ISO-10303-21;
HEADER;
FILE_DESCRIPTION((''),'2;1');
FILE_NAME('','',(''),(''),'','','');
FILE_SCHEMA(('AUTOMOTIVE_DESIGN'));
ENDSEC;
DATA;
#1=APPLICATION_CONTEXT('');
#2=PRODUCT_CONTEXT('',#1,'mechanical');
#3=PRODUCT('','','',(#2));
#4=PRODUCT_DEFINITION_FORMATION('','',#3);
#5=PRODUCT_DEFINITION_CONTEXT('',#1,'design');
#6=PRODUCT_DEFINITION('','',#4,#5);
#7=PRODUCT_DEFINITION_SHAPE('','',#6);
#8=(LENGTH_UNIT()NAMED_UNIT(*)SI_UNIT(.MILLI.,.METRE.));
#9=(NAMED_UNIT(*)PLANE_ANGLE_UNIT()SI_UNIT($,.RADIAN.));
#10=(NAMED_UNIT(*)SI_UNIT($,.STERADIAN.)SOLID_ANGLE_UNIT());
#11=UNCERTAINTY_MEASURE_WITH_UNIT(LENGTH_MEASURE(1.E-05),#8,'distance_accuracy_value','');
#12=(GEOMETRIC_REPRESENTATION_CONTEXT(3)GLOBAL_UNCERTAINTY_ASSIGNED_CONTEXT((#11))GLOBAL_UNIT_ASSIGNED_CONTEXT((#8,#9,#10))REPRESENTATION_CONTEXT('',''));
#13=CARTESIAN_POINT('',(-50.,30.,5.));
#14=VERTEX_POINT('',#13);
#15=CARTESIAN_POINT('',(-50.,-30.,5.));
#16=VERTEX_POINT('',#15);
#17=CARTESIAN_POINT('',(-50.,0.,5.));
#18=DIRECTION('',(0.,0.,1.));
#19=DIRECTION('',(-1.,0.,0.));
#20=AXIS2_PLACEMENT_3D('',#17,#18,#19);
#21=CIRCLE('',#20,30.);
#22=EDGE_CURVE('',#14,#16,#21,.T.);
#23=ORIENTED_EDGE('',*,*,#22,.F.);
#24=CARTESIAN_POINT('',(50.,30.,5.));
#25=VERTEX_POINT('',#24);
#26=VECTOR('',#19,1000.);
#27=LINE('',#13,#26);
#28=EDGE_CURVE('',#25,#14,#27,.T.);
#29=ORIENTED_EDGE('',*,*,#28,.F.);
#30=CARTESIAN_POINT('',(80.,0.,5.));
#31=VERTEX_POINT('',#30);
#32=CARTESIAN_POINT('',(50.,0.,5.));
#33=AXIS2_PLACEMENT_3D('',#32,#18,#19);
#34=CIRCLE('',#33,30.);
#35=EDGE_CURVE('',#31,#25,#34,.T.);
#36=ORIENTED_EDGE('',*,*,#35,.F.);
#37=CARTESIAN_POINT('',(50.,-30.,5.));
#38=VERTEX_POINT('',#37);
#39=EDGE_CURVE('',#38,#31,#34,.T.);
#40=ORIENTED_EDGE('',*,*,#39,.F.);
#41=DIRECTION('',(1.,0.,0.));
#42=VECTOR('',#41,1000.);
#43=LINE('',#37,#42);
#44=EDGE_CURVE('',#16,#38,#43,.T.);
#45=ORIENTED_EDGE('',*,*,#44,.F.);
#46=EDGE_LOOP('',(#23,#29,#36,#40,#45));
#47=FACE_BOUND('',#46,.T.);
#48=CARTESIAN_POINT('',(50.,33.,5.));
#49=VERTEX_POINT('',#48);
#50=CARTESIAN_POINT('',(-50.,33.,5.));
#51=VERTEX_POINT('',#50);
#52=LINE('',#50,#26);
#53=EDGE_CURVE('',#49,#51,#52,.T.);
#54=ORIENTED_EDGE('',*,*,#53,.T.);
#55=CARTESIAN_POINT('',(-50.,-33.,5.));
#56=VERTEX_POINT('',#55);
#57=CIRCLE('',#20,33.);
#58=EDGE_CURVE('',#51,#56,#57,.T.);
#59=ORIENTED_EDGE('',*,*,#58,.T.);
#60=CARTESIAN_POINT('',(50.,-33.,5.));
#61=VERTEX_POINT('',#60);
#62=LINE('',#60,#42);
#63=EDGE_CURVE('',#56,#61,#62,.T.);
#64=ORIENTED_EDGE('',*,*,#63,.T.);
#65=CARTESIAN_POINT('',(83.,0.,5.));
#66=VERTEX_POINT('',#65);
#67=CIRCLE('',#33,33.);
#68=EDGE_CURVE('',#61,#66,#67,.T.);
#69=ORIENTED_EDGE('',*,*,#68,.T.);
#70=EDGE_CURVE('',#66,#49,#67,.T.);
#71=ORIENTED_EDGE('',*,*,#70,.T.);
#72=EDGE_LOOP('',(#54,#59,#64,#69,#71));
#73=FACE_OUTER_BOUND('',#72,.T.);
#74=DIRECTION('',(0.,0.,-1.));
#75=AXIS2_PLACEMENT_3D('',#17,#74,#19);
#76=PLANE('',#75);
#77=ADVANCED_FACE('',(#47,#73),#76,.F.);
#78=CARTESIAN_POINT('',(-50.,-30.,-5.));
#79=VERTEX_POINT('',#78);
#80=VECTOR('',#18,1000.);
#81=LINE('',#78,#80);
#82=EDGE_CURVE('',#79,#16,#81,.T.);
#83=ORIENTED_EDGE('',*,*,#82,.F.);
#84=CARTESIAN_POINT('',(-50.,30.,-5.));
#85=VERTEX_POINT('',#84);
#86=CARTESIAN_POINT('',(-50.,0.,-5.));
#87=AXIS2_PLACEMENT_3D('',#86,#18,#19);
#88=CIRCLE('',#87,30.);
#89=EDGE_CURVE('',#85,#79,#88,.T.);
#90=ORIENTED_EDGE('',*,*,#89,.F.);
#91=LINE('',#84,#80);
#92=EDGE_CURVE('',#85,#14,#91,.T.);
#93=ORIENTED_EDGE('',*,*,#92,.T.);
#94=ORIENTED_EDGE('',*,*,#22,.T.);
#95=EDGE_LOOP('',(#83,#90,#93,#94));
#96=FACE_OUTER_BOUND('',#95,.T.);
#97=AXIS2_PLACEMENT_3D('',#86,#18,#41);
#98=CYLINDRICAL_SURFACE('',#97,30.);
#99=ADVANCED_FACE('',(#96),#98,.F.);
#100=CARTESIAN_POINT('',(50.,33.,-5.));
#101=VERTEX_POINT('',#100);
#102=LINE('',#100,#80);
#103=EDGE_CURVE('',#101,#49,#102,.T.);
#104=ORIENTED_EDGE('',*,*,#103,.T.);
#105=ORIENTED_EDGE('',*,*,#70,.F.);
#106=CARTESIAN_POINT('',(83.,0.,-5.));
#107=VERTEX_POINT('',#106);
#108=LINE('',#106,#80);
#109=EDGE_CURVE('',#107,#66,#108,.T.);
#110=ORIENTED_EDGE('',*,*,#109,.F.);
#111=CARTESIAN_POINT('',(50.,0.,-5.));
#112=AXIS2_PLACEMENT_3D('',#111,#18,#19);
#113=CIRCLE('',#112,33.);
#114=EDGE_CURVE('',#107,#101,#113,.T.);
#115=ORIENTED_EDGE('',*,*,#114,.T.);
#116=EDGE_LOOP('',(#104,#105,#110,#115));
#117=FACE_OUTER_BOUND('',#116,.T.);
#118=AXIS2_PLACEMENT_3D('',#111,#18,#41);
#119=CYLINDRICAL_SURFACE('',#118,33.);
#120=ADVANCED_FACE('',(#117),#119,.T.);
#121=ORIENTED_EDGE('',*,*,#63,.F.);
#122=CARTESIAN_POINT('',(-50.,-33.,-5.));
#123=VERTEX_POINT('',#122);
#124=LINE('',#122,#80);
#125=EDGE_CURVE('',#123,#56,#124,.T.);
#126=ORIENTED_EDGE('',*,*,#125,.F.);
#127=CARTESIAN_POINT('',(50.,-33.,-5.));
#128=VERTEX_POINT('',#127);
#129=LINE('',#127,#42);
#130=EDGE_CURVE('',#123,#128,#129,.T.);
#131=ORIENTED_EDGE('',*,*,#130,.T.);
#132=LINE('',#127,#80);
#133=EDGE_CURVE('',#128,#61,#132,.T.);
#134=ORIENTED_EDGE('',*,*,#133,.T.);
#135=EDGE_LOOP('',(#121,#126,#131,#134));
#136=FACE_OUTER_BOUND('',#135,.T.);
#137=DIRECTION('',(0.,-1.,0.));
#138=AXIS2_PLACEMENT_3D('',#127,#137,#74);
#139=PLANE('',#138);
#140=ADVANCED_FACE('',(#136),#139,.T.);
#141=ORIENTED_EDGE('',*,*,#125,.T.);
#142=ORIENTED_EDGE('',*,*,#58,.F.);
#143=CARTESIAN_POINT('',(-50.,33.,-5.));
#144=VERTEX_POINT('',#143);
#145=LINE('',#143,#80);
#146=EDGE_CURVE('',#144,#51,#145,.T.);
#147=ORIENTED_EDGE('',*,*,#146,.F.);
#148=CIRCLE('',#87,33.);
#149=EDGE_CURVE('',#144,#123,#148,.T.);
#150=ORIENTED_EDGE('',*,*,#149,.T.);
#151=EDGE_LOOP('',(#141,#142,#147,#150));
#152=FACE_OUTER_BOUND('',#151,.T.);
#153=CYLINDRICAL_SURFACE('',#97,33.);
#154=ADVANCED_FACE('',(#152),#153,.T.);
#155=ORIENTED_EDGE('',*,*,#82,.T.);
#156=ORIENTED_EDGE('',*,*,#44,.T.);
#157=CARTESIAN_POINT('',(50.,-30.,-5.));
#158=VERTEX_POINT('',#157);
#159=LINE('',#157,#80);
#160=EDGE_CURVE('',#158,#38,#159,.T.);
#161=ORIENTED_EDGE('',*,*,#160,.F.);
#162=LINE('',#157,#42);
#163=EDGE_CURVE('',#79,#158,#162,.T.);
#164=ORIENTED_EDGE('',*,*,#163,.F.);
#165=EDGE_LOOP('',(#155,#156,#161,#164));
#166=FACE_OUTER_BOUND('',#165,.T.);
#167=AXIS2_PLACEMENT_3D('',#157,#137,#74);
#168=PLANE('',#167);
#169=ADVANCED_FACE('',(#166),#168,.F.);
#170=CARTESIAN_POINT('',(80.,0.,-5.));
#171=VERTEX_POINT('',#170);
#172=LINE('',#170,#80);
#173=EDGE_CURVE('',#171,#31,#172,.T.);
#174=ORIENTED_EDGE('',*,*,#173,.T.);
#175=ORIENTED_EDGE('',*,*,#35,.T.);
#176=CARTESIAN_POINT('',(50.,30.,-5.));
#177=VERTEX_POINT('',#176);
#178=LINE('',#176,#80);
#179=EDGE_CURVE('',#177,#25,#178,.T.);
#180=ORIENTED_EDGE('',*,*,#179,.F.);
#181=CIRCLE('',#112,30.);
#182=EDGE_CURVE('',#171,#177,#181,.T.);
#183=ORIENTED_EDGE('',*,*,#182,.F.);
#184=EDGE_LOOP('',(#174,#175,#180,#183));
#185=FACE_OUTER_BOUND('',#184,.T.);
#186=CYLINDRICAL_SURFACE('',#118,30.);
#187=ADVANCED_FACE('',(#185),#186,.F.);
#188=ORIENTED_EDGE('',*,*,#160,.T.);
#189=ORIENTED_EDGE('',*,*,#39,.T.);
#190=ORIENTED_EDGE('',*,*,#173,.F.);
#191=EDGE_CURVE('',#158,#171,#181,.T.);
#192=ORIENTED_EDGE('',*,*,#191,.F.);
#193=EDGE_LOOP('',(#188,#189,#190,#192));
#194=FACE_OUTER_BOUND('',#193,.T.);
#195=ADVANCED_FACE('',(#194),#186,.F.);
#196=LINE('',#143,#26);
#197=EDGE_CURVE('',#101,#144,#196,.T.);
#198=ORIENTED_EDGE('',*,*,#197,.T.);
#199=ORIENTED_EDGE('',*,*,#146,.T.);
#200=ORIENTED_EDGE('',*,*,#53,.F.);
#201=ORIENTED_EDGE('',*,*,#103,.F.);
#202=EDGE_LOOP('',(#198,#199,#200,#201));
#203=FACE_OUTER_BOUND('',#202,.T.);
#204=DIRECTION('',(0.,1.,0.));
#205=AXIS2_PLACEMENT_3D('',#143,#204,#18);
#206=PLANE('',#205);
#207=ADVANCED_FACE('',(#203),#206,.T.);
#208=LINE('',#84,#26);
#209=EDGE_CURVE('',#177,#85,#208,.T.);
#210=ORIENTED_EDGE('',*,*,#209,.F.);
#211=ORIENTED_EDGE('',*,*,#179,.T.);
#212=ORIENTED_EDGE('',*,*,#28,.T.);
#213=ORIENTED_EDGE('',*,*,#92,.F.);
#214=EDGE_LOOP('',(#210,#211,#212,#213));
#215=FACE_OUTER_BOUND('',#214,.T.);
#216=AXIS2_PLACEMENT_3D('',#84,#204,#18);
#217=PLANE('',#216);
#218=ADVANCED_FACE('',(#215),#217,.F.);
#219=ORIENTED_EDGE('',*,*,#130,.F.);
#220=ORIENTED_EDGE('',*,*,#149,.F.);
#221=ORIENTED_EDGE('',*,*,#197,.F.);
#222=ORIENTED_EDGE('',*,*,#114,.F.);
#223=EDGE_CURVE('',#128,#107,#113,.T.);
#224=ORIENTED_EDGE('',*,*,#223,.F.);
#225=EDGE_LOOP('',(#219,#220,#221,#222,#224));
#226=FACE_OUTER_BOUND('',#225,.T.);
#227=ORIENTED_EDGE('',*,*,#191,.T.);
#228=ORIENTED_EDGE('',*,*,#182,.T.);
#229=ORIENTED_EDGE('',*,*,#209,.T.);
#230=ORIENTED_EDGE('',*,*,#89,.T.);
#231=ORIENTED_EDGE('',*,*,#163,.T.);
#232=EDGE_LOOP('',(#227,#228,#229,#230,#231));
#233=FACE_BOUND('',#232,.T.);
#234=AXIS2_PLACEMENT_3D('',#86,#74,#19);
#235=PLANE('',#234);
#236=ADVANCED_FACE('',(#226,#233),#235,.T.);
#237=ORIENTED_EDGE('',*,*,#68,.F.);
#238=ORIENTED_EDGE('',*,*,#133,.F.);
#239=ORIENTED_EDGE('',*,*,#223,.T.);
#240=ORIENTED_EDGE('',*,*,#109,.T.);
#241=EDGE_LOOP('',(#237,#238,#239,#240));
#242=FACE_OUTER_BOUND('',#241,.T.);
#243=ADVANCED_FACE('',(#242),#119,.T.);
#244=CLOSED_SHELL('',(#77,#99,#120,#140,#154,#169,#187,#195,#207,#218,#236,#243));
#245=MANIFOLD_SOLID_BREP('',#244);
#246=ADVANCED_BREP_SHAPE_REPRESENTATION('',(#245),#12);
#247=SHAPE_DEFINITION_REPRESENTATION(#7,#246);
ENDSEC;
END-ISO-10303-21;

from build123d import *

# Parameters (mm, degrees)
EXTRUDE_1_DEPTH = 5


with BuildPart() as part:
    # 草图1 → 凸台-拉伸1 (new, symmetric)
    with BuildSketch(Plane.XY):
        with BuildLine():
            Line((-50, 33), (50, 33))
            ThreePointArc((50, 33), (83, 0), (50, -33))
            Line((50, -33), (-50, -33))
            ThreePointArc((-50, -33), (-83, 0), (-50, 33))
        make_face()
        with BuildLine():
            Line((-50, 30), (50, 30))
            ThreePointArc((50, 30), (80, 0), (50, -30))
            Line((50, -30), (-50, -30))
            ThreePointArc((-50, -30), (-80, 0), (-50, 30))
        make_face(mode=Mode.SUBTRACT)
    extrude(amount=EXTRUDE_1_DEPTH, both=True)


solid = part.part
